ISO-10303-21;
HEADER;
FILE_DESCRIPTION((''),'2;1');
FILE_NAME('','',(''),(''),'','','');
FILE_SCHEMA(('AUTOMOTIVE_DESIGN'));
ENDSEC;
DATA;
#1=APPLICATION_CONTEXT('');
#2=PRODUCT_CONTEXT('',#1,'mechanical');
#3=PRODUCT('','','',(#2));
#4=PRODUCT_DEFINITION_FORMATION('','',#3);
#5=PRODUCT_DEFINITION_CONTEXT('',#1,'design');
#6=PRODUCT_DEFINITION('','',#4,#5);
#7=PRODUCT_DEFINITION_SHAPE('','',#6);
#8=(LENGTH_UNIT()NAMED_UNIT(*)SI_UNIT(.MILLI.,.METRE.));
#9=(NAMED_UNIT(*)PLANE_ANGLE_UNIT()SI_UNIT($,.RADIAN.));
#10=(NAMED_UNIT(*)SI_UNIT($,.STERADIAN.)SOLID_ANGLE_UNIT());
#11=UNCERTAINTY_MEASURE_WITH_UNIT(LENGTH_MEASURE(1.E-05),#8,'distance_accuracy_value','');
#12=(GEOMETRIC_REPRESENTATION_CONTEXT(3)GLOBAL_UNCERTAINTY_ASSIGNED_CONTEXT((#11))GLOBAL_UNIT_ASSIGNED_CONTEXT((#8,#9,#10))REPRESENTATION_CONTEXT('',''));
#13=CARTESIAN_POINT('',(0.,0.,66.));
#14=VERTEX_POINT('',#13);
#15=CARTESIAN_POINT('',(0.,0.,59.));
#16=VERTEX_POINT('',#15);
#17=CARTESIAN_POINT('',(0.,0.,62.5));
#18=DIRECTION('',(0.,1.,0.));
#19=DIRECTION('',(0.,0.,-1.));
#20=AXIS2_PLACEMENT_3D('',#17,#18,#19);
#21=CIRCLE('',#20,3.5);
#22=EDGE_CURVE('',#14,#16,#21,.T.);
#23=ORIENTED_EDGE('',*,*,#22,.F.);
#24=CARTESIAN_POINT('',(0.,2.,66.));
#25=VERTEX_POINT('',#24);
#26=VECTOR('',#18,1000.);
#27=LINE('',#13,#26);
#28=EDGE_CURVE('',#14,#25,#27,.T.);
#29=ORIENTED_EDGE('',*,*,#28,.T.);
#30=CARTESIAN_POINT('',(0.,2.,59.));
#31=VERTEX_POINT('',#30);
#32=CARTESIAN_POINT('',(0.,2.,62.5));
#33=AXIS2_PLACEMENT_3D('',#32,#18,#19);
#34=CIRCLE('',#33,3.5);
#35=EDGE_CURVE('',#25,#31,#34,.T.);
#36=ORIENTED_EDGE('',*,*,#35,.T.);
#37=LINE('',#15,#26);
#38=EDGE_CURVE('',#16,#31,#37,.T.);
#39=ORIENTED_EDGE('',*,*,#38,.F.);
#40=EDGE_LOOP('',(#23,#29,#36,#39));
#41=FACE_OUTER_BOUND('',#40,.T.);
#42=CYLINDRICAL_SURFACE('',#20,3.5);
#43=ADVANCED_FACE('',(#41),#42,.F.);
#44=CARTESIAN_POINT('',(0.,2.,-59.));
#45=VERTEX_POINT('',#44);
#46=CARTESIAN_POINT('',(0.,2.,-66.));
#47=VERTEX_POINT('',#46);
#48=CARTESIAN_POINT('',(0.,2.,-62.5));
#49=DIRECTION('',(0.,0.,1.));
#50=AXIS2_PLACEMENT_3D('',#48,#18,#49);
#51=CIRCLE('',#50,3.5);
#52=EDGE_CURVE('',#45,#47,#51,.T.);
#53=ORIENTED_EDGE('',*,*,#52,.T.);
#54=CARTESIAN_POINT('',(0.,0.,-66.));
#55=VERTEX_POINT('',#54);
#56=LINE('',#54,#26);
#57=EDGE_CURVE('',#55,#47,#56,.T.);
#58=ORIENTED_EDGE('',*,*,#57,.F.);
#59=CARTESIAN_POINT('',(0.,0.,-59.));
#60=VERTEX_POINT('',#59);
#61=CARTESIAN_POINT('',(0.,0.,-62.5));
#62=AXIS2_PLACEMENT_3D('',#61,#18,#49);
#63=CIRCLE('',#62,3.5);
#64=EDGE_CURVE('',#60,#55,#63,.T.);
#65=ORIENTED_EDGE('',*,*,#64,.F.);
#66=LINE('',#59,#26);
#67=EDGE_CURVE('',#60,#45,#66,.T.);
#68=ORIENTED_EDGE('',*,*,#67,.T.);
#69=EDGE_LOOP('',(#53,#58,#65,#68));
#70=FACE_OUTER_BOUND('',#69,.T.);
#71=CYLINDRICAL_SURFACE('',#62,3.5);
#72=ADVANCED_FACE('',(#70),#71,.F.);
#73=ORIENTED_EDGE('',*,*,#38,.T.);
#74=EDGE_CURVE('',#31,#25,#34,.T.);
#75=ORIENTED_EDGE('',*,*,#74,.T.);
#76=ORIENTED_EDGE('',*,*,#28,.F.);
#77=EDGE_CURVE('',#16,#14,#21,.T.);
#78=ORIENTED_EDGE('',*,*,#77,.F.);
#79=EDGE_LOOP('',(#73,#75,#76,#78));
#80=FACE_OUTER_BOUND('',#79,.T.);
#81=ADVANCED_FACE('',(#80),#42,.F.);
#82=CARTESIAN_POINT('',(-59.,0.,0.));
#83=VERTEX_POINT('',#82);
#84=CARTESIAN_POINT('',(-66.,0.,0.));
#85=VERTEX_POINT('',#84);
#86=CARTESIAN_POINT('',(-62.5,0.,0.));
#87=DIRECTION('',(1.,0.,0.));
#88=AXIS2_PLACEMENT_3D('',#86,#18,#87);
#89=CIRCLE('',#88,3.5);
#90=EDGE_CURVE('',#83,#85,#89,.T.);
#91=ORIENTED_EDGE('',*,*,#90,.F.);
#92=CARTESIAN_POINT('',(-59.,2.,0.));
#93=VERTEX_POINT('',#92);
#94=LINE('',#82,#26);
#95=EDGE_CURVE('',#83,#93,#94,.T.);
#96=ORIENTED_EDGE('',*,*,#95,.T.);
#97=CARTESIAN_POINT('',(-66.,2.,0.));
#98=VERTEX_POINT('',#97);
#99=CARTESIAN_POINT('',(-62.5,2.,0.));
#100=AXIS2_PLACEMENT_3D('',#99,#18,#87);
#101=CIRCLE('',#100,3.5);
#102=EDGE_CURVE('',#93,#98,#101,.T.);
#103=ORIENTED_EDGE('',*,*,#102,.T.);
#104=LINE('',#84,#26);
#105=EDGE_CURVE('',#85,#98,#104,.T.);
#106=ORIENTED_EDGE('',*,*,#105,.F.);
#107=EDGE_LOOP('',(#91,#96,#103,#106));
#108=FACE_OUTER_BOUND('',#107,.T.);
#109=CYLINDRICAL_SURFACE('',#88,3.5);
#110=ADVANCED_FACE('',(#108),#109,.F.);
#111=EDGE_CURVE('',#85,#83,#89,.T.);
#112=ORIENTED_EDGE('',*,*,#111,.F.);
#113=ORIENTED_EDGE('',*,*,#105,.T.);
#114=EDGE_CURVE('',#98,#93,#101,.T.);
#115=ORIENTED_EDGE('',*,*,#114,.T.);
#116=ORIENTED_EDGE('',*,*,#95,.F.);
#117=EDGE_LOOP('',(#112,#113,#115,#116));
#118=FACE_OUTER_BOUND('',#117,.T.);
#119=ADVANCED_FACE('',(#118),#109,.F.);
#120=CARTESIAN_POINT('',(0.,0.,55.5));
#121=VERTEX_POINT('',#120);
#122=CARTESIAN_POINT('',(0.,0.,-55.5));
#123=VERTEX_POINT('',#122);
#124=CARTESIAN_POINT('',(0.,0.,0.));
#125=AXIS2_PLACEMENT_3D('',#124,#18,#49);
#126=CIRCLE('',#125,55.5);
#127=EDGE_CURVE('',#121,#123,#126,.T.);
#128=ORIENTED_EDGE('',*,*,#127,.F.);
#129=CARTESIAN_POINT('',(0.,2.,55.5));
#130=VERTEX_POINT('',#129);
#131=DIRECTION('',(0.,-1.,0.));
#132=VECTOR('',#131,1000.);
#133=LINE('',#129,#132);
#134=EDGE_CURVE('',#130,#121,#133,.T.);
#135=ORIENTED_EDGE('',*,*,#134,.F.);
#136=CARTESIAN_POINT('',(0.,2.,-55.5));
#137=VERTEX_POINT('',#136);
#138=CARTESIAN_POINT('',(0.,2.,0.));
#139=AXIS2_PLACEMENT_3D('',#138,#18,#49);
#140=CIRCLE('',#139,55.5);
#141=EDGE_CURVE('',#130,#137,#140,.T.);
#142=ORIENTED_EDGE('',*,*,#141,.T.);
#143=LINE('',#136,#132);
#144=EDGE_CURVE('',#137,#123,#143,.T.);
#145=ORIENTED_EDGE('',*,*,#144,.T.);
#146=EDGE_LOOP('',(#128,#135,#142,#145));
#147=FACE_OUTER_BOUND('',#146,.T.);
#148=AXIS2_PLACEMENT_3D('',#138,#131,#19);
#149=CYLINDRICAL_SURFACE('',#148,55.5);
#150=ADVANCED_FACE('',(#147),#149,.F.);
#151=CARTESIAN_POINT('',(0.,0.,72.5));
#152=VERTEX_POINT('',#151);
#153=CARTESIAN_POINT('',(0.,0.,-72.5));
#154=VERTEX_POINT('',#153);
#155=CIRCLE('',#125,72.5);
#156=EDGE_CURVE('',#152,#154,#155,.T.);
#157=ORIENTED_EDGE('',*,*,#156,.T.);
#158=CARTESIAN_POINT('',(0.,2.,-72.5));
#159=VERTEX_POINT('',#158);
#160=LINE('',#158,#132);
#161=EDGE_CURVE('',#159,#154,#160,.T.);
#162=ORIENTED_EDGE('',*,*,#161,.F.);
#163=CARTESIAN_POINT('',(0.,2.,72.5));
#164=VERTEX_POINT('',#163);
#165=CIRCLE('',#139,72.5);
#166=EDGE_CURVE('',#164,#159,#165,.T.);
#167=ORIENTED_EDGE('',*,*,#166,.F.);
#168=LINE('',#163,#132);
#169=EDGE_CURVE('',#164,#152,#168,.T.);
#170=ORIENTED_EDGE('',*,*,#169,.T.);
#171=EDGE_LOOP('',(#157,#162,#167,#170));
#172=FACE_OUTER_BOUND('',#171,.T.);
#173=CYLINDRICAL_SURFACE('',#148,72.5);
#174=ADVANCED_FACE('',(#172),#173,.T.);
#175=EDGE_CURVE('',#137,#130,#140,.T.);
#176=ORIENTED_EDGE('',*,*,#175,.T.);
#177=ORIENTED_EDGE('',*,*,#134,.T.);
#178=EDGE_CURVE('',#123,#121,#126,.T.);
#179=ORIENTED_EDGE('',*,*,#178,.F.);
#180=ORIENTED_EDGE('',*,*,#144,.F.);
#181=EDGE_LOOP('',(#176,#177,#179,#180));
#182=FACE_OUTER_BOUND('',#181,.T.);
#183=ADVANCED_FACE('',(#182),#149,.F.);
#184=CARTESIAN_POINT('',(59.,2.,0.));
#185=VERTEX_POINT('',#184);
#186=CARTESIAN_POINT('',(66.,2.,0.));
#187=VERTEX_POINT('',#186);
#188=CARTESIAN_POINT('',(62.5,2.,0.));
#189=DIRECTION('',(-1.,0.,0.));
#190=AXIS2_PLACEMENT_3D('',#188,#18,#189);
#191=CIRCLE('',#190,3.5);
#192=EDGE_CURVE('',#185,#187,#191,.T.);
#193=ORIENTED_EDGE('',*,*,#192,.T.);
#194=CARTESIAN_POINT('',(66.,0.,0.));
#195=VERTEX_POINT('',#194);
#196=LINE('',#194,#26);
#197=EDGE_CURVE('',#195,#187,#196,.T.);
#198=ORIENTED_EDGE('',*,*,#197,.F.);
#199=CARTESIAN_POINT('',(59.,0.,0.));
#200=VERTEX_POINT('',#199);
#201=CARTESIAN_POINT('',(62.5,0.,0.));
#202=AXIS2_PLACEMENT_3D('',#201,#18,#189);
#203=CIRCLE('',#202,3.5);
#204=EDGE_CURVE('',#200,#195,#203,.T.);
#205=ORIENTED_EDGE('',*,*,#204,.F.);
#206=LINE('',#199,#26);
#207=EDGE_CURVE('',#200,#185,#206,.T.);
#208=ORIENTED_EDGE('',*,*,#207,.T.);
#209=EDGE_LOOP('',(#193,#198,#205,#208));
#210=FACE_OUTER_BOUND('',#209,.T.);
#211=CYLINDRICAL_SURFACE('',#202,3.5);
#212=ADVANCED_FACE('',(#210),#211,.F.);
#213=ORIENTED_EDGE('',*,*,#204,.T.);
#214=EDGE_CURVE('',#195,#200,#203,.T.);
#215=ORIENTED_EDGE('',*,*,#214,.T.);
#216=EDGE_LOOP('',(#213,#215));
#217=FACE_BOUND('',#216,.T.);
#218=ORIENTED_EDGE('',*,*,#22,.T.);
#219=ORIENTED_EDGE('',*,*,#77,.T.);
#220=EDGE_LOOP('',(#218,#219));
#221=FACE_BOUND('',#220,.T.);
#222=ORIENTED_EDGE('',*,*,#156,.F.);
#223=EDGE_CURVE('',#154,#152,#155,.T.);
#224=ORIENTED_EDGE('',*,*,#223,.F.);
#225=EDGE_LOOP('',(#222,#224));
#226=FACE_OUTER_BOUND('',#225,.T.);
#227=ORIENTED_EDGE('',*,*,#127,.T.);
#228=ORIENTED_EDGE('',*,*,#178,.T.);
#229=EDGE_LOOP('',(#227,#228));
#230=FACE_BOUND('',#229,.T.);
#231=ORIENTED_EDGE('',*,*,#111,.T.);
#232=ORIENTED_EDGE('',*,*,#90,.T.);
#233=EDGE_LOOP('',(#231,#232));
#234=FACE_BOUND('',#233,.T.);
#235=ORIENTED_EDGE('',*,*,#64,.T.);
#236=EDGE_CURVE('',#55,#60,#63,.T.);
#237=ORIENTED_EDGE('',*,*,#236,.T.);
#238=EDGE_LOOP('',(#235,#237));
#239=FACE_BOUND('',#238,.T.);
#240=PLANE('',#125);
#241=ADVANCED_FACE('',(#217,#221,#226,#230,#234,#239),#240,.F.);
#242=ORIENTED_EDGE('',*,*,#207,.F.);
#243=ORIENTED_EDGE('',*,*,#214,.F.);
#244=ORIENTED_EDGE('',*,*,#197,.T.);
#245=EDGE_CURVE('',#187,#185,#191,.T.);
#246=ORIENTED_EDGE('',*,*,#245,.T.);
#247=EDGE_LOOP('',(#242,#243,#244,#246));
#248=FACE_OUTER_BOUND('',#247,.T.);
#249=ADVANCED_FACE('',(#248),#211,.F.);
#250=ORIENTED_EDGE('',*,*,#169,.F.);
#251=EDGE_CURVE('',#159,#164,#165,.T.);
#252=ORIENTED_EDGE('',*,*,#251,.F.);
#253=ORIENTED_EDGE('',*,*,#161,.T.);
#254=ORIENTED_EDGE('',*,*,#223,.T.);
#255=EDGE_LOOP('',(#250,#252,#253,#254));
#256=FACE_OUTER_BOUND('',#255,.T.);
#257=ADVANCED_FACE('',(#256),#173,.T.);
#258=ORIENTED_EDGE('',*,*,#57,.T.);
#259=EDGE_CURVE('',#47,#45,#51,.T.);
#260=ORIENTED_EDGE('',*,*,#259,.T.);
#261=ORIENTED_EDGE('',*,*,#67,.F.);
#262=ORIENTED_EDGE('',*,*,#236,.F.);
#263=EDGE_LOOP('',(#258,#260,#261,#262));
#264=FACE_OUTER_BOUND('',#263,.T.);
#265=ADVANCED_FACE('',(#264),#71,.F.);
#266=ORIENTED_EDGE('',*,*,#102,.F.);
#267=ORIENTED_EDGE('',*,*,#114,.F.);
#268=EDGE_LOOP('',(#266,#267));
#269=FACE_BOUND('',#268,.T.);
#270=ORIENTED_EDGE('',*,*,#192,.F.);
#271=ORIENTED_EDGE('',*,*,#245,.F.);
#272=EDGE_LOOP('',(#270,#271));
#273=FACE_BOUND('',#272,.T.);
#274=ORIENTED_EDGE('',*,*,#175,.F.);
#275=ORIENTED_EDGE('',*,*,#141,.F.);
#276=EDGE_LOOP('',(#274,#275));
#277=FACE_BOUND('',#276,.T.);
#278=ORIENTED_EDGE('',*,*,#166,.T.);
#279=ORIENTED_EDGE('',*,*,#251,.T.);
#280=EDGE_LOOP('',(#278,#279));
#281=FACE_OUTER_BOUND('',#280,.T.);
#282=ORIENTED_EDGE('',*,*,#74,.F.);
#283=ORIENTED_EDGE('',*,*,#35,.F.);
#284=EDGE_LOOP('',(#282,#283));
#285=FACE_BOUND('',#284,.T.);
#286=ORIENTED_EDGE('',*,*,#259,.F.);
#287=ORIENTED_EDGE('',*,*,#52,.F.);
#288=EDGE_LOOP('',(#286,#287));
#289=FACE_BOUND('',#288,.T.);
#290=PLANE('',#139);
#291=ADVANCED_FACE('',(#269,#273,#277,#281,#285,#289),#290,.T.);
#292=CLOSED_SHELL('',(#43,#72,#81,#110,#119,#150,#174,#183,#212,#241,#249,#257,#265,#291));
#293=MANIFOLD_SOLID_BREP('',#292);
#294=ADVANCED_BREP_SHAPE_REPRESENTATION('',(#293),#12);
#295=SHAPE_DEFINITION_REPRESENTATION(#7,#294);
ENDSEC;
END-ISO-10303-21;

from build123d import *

# Parameters (mm, degrees)
SKETCH1_R           = 72.5
SKETCH1_R_2         = 55.5
BOSS_EXTRUDE1_DEPTH = 2
SKETCH2_R           = 3.5
CUT_EXTRUDE1_DEPTH  = 103.549987811
CIRPATTERN1_COUNT   = 4


with BuildPart() as part:
    # Sketch1 → Boss-Extrude1 (new body)
    with BuildSketch(Plane(origin=(0, 0, 0), x_dir=(1, 0, 0), z_dir=(0, 1, 0))):
        with Locations(Location((0, 0, 0), (0, 0, 270))):
            Circle(SKETCH1_R)
        with Locations(Location((0, 0, 0), (0, 0, 270))):
            Circle(SKETCH1_R_2, mode=Mode.SUBTRACT)
    extrude(amount=BOSS_EXTRUDE1_DEPTH)

    # Sketch2 → Cut-Extrude1 (cut, through all)
    with BuildSketch(Plane(origin=(0, 2, 0), x_dir=(1, 0, 0), z_dir=(0, 1, 0))):
        with Locations(Location((0, 62.5, 0), (0, 0, 270))):
            Circle(SKETCH2_R)
    cut_extrude1 = extrude(amount=-CUT_EXTRUDE1_DEPTH, mode=Mode.SUBTRACT)

    # CirPattern1: Cut-Extrude1 ×4 about axis
    cirpattern1_axis = Axis((0, 0, 0), (0, 1, 0))
    for i in range(1, CIRPATTERN1_COUNT):
        add(cut_extrude1.rotate(cirpattern1_axis, i * 360 / CIRPATTERN1_COUNT), mode=Mode.SUBTRACT)


solid = part.part
